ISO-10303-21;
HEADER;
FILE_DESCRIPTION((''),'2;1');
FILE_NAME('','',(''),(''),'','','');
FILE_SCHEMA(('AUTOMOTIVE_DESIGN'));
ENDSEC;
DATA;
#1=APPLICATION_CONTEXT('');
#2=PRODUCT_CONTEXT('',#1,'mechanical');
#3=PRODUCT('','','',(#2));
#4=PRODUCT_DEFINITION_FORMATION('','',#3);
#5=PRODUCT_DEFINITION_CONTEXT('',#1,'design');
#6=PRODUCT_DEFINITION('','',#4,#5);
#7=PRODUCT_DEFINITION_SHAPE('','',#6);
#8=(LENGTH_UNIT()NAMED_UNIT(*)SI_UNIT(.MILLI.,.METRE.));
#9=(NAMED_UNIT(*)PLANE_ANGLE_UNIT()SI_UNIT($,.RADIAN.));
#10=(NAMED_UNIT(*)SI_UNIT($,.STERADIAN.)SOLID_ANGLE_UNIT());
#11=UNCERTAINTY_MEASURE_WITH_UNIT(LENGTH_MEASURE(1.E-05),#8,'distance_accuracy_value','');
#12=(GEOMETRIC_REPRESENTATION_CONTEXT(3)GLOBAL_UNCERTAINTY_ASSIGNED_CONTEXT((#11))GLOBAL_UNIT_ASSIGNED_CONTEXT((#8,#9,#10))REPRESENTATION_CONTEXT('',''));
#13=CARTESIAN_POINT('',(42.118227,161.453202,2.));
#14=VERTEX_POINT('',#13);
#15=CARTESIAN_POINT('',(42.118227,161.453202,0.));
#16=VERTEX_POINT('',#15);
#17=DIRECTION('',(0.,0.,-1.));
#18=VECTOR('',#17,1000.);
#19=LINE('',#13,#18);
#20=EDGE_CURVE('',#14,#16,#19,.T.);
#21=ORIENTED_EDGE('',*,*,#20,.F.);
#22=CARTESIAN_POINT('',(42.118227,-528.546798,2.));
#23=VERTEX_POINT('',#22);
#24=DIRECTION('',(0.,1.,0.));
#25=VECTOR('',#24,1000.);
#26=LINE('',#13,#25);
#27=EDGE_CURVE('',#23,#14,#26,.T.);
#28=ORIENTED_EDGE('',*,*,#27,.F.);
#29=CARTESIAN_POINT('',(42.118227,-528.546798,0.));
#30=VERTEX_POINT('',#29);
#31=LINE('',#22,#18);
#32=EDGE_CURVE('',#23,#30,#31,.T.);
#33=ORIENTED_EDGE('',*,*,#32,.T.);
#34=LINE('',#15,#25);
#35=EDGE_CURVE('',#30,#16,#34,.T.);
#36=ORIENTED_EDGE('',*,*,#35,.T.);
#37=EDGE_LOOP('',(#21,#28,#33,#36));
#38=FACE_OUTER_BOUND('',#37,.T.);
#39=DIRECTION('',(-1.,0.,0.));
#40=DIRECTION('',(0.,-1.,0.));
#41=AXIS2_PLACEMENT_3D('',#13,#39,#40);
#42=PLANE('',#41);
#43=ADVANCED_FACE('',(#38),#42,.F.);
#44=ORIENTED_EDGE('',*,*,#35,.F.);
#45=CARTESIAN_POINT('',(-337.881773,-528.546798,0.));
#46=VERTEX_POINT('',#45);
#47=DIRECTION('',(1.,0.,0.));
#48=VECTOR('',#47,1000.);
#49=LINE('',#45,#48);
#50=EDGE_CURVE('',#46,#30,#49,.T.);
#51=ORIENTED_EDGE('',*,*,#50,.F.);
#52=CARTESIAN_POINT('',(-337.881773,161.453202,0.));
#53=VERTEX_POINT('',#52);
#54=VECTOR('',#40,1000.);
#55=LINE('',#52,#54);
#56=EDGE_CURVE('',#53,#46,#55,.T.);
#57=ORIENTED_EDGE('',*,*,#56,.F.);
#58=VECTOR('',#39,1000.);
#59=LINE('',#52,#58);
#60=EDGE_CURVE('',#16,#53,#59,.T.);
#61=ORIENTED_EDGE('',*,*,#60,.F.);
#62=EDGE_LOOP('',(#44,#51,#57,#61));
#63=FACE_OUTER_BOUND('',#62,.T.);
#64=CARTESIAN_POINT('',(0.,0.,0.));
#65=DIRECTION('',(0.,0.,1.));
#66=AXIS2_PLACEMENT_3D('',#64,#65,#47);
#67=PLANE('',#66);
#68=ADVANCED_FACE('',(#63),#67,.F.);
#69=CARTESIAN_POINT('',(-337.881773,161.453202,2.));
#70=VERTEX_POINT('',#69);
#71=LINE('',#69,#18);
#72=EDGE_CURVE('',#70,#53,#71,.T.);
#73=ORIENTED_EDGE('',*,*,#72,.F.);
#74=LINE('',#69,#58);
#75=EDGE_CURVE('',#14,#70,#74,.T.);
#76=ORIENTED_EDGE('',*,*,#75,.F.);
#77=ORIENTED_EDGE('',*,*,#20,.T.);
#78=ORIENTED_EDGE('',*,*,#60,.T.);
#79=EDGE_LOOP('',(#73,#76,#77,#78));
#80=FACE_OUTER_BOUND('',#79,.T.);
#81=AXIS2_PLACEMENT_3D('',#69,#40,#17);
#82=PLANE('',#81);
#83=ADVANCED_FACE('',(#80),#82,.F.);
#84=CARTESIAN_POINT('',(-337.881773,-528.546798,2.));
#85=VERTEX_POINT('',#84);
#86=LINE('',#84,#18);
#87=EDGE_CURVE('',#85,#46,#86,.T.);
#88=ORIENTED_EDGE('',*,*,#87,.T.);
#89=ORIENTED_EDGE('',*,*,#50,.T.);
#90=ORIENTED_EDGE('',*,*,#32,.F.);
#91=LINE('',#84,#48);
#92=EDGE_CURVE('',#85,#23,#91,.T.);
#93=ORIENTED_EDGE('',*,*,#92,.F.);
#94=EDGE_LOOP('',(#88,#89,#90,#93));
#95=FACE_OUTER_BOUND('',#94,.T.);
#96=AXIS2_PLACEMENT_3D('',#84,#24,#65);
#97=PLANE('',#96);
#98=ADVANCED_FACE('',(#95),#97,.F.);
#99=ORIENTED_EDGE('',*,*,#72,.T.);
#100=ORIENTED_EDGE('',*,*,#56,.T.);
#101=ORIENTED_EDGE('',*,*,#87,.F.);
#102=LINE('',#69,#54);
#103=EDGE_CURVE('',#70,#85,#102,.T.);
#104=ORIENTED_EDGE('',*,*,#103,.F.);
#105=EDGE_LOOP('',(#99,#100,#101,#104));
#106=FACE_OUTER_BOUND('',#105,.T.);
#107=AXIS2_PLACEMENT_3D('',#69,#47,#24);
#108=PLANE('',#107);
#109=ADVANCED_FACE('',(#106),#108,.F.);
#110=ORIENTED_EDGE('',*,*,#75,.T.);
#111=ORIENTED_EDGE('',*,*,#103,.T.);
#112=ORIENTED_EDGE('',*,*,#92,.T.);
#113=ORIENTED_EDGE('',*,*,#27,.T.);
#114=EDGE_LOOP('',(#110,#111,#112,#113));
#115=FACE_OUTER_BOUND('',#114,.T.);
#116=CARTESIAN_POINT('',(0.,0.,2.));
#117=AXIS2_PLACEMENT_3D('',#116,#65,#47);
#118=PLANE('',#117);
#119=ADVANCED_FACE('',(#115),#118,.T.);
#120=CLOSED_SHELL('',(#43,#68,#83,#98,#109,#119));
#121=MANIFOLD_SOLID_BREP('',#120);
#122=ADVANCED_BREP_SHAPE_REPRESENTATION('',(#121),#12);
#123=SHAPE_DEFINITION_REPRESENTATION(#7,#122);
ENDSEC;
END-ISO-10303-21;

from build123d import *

# Parameters (mm, degrees)
SKETCH_1_W      = 380
SKETCH_1_H      = 690
EXTRUDE_1_DEPTH = 2


with BuildPart() as part:
    # 草图1 → 凸台-拉伸1 (new body)
    with BuildSketch(Plane.XY):
        with Locations((-147.881773399, -183.54679803)):
            Rectangle(SKETCH_1_W, SKETCH_1_H)
    extrude(amount=EXTRUDE_1_DEPTH)


solid = part.part
